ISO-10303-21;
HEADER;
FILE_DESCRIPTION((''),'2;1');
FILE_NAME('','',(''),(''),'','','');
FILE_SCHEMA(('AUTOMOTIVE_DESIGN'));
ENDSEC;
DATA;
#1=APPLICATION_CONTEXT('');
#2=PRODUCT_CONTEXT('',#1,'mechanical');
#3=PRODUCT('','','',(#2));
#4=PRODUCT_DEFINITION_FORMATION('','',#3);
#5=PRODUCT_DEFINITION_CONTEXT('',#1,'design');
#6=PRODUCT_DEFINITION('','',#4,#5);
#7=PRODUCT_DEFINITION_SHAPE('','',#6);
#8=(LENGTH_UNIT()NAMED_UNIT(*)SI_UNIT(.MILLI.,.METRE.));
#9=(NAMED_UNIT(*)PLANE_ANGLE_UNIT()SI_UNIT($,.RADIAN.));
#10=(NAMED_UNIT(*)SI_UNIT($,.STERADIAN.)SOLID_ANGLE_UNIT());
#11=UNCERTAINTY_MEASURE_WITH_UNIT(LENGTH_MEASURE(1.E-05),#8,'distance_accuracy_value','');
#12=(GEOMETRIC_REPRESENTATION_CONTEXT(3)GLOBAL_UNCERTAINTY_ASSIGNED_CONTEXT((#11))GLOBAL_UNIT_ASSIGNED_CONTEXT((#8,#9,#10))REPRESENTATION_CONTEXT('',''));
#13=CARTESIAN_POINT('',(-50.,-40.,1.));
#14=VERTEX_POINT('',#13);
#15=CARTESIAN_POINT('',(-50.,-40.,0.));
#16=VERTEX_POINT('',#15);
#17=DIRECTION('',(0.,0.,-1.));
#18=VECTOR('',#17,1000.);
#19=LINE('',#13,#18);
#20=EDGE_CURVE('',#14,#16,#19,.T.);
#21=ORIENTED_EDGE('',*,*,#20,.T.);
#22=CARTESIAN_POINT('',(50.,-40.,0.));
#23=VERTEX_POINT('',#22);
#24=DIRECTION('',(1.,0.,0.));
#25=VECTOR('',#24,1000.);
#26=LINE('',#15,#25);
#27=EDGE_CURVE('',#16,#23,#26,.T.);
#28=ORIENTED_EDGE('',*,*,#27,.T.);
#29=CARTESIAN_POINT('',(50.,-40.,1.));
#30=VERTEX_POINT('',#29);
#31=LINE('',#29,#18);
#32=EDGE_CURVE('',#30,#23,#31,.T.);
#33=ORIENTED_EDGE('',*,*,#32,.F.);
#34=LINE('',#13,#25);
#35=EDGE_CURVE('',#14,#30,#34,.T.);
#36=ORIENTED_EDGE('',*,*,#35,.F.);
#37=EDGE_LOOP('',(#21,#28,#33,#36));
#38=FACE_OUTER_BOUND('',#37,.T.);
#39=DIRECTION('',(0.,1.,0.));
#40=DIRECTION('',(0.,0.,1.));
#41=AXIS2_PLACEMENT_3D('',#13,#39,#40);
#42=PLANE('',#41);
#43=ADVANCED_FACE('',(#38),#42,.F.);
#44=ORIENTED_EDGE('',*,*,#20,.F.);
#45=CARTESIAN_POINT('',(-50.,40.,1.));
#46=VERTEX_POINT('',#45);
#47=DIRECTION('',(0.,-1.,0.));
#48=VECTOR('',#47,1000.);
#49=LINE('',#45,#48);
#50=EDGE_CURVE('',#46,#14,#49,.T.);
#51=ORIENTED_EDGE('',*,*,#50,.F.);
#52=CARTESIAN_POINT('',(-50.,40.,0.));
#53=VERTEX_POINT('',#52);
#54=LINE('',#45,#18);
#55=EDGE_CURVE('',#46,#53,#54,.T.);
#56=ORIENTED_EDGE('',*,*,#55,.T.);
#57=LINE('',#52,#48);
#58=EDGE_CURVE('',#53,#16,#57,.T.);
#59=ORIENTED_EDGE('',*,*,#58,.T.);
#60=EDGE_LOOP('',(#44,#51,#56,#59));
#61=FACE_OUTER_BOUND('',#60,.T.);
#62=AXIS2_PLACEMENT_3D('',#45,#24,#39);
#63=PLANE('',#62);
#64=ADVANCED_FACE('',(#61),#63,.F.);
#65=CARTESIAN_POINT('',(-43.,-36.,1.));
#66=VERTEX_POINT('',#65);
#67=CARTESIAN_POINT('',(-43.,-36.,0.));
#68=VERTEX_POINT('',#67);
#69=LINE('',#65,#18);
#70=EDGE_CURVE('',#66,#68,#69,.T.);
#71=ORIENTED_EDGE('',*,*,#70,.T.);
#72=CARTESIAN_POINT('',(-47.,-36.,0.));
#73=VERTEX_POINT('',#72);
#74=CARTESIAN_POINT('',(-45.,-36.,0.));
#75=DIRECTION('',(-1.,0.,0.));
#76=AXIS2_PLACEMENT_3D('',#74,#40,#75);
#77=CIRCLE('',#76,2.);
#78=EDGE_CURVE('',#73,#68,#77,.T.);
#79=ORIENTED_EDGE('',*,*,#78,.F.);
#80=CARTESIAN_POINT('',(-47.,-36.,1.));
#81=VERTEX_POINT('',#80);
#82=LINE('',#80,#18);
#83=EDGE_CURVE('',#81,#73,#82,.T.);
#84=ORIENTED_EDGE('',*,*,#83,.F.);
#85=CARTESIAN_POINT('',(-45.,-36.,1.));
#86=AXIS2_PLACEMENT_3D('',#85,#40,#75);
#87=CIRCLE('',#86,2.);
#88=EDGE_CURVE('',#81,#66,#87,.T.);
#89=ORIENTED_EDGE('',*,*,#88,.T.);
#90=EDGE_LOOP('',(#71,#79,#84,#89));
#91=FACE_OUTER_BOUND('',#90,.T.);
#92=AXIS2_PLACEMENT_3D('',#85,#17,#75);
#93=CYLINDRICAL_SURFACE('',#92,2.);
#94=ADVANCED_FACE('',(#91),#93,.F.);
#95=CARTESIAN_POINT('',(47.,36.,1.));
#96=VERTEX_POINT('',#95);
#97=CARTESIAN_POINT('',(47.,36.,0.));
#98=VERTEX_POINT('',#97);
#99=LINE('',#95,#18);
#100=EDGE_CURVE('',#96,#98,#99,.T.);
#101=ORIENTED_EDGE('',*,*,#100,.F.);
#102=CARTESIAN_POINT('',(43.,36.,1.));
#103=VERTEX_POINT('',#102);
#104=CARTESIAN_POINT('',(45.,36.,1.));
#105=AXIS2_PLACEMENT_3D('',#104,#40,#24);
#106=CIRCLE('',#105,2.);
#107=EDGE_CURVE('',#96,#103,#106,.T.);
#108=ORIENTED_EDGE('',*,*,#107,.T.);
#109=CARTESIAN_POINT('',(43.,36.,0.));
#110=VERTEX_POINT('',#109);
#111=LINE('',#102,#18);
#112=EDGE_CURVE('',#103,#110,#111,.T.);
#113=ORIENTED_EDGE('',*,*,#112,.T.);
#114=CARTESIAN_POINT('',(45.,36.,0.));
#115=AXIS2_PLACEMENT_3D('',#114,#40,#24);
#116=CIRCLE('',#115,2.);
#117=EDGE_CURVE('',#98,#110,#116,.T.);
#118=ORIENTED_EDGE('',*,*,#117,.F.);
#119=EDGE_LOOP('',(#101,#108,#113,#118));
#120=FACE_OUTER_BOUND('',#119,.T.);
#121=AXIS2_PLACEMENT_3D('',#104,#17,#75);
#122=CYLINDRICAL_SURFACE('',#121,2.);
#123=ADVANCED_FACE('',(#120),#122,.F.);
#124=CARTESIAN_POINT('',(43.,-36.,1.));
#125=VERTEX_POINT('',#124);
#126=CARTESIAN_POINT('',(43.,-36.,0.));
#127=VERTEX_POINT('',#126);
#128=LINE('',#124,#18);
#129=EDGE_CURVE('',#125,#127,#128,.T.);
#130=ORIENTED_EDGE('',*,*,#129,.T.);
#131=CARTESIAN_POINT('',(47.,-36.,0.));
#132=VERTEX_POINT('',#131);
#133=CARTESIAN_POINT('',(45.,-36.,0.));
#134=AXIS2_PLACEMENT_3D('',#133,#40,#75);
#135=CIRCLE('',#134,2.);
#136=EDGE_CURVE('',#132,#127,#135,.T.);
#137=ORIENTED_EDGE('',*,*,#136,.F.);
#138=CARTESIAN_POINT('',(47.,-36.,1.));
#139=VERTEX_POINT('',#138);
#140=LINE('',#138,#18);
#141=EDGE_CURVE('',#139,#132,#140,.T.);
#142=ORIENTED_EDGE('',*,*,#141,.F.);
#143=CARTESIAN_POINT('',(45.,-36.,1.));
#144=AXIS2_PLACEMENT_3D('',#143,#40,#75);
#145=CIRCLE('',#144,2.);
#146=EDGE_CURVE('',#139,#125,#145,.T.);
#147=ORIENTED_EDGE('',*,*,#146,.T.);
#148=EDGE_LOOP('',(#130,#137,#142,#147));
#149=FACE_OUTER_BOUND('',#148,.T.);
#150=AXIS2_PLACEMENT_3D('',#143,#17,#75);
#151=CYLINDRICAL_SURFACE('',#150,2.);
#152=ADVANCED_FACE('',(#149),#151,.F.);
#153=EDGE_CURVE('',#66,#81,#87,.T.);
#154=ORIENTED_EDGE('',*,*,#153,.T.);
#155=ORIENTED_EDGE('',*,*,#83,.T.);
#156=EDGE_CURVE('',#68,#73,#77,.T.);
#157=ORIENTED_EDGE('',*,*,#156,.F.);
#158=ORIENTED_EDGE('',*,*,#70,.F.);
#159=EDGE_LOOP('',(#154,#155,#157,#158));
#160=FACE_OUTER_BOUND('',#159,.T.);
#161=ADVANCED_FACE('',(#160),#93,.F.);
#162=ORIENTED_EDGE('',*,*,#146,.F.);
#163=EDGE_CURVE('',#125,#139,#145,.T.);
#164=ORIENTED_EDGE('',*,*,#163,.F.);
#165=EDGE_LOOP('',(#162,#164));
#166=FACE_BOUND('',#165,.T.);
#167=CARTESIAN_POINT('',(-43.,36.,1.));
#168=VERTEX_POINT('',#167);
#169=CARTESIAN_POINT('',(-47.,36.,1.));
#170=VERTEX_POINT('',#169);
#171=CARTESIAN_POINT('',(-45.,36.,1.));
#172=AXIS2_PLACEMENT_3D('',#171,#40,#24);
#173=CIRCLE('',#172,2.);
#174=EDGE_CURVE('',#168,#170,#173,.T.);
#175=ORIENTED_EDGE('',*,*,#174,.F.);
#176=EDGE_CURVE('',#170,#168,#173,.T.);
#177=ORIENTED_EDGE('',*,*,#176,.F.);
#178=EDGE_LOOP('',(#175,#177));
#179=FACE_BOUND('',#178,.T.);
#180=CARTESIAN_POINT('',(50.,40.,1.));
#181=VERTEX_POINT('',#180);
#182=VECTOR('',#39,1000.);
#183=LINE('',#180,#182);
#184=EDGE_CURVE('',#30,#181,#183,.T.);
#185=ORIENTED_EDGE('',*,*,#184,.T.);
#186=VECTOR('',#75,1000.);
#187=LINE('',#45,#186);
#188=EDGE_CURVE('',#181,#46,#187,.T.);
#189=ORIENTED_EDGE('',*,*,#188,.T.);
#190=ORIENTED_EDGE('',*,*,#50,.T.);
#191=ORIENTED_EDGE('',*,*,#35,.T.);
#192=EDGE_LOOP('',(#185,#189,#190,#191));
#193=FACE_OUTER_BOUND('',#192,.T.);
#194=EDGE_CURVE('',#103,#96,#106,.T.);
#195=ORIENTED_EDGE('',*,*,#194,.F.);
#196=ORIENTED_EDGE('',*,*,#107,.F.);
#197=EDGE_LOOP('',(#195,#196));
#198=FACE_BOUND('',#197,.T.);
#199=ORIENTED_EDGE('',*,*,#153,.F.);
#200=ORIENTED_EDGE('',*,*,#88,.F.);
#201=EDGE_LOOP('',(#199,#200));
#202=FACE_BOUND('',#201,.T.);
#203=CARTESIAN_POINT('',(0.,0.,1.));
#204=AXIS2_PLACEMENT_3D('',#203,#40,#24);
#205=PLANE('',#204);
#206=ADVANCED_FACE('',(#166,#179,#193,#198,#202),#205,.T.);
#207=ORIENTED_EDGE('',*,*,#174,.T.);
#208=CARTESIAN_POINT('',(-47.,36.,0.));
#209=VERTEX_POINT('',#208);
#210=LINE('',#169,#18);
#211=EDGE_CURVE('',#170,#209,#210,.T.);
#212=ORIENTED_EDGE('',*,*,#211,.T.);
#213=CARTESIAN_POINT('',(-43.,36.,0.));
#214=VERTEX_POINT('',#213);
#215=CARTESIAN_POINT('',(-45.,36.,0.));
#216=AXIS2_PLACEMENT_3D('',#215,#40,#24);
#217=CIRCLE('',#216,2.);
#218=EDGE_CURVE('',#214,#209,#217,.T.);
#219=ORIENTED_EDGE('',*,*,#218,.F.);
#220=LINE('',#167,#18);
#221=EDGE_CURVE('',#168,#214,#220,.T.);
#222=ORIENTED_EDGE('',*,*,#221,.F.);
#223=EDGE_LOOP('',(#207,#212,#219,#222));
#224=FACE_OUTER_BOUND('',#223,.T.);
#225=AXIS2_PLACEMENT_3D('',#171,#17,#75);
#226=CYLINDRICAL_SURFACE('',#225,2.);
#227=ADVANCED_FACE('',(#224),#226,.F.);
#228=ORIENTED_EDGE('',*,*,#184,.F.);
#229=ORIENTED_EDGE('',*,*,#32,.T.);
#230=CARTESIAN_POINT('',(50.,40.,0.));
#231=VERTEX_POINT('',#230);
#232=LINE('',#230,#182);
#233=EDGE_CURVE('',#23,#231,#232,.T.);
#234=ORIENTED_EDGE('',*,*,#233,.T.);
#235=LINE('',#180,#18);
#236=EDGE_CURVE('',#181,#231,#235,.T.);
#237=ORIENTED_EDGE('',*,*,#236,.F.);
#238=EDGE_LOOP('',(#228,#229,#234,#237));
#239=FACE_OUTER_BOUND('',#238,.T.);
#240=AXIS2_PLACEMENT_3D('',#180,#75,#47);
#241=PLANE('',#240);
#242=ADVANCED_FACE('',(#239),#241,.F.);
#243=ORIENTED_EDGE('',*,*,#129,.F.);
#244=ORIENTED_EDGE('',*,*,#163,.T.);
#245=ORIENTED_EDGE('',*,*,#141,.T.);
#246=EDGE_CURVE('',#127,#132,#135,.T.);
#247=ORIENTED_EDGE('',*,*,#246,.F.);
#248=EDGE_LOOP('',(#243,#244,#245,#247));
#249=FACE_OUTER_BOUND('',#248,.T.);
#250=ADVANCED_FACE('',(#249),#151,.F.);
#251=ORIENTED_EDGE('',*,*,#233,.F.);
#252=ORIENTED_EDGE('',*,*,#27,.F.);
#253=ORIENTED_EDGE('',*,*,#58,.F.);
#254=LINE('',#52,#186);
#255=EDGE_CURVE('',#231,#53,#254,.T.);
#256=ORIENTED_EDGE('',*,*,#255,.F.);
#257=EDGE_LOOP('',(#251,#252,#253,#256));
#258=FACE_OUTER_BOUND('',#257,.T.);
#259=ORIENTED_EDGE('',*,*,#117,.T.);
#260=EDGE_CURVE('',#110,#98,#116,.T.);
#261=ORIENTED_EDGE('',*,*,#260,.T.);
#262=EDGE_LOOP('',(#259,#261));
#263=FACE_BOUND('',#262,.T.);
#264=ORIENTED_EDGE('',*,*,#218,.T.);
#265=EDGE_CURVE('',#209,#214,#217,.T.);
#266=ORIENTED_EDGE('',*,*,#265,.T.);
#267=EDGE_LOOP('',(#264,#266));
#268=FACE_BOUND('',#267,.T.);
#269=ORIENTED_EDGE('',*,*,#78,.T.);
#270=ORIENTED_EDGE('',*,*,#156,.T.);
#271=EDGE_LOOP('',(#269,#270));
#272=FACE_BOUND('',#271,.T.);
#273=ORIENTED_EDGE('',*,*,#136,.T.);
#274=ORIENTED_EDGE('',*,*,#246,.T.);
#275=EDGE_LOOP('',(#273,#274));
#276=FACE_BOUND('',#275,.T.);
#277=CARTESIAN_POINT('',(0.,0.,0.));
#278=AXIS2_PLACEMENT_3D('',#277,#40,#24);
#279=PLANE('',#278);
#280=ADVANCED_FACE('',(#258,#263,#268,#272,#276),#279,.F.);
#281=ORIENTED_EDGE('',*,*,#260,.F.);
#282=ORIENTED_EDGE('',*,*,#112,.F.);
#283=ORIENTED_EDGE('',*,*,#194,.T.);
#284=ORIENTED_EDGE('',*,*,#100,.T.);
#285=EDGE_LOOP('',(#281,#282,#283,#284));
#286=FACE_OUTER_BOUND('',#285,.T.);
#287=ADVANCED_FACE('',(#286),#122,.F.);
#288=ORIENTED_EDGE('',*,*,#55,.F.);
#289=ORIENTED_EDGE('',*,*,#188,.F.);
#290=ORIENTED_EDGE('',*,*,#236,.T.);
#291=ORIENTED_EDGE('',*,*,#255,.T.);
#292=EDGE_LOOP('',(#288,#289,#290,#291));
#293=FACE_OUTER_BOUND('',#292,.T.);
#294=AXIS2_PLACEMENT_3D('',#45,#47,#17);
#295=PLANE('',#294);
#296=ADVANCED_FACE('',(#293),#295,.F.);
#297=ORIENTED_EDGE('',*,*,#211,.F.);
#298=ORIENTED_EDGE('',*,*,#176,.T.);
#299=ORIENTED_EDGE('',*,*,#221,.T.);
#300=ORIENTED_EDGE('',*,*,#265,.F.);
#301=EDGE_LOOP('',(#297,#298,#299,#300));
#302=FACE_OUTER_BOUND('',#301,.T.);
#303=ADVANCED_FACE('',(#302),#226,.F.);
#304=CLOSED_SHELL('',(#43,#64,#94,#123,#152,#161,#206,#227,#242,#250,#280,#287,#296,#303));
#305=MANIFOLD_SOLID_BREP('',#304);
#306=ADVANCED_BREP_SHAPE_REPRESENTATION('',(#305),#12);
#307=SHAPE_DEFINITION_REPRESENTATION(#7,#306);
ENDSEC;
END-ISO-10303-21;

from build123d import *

# Parameters (mm, degrees)
SKETCH1_W           = 100
SKETCH1_H           = 80
SKETCH1_R           = 2
BOSS_EXTRUDE1_DEPTH = 1


with BuildPart() as part:
    # Sketch1 → Boss-Extrude1 (new body)
    with BuildSketch(Plane.XY):
        Rectangle(SKETCH1_W, SKETCH1_H)
        with Locations((45, 36)):
            Circle(SKETCH1_R, mode=Mode.SUBTRACT)
        with Locations((-45, 36)):
            Circle(SKETCH1_R, mode=Mode.SUBTRACT)
        with Locations(Location((-45, -36, 0), (0, 0, 180))):
            Circle(SKETCH1_R, mode=Mode.SUBTRACT)
        with Locations(Location((45, -36, 0), (0, 0, 180))):
            Circle(SKETCH1_R, mode=Mode.SUBTRACT)
    extrude(amount=BOSS_EXTRUDE1_DEPTH)


solid = part.part
